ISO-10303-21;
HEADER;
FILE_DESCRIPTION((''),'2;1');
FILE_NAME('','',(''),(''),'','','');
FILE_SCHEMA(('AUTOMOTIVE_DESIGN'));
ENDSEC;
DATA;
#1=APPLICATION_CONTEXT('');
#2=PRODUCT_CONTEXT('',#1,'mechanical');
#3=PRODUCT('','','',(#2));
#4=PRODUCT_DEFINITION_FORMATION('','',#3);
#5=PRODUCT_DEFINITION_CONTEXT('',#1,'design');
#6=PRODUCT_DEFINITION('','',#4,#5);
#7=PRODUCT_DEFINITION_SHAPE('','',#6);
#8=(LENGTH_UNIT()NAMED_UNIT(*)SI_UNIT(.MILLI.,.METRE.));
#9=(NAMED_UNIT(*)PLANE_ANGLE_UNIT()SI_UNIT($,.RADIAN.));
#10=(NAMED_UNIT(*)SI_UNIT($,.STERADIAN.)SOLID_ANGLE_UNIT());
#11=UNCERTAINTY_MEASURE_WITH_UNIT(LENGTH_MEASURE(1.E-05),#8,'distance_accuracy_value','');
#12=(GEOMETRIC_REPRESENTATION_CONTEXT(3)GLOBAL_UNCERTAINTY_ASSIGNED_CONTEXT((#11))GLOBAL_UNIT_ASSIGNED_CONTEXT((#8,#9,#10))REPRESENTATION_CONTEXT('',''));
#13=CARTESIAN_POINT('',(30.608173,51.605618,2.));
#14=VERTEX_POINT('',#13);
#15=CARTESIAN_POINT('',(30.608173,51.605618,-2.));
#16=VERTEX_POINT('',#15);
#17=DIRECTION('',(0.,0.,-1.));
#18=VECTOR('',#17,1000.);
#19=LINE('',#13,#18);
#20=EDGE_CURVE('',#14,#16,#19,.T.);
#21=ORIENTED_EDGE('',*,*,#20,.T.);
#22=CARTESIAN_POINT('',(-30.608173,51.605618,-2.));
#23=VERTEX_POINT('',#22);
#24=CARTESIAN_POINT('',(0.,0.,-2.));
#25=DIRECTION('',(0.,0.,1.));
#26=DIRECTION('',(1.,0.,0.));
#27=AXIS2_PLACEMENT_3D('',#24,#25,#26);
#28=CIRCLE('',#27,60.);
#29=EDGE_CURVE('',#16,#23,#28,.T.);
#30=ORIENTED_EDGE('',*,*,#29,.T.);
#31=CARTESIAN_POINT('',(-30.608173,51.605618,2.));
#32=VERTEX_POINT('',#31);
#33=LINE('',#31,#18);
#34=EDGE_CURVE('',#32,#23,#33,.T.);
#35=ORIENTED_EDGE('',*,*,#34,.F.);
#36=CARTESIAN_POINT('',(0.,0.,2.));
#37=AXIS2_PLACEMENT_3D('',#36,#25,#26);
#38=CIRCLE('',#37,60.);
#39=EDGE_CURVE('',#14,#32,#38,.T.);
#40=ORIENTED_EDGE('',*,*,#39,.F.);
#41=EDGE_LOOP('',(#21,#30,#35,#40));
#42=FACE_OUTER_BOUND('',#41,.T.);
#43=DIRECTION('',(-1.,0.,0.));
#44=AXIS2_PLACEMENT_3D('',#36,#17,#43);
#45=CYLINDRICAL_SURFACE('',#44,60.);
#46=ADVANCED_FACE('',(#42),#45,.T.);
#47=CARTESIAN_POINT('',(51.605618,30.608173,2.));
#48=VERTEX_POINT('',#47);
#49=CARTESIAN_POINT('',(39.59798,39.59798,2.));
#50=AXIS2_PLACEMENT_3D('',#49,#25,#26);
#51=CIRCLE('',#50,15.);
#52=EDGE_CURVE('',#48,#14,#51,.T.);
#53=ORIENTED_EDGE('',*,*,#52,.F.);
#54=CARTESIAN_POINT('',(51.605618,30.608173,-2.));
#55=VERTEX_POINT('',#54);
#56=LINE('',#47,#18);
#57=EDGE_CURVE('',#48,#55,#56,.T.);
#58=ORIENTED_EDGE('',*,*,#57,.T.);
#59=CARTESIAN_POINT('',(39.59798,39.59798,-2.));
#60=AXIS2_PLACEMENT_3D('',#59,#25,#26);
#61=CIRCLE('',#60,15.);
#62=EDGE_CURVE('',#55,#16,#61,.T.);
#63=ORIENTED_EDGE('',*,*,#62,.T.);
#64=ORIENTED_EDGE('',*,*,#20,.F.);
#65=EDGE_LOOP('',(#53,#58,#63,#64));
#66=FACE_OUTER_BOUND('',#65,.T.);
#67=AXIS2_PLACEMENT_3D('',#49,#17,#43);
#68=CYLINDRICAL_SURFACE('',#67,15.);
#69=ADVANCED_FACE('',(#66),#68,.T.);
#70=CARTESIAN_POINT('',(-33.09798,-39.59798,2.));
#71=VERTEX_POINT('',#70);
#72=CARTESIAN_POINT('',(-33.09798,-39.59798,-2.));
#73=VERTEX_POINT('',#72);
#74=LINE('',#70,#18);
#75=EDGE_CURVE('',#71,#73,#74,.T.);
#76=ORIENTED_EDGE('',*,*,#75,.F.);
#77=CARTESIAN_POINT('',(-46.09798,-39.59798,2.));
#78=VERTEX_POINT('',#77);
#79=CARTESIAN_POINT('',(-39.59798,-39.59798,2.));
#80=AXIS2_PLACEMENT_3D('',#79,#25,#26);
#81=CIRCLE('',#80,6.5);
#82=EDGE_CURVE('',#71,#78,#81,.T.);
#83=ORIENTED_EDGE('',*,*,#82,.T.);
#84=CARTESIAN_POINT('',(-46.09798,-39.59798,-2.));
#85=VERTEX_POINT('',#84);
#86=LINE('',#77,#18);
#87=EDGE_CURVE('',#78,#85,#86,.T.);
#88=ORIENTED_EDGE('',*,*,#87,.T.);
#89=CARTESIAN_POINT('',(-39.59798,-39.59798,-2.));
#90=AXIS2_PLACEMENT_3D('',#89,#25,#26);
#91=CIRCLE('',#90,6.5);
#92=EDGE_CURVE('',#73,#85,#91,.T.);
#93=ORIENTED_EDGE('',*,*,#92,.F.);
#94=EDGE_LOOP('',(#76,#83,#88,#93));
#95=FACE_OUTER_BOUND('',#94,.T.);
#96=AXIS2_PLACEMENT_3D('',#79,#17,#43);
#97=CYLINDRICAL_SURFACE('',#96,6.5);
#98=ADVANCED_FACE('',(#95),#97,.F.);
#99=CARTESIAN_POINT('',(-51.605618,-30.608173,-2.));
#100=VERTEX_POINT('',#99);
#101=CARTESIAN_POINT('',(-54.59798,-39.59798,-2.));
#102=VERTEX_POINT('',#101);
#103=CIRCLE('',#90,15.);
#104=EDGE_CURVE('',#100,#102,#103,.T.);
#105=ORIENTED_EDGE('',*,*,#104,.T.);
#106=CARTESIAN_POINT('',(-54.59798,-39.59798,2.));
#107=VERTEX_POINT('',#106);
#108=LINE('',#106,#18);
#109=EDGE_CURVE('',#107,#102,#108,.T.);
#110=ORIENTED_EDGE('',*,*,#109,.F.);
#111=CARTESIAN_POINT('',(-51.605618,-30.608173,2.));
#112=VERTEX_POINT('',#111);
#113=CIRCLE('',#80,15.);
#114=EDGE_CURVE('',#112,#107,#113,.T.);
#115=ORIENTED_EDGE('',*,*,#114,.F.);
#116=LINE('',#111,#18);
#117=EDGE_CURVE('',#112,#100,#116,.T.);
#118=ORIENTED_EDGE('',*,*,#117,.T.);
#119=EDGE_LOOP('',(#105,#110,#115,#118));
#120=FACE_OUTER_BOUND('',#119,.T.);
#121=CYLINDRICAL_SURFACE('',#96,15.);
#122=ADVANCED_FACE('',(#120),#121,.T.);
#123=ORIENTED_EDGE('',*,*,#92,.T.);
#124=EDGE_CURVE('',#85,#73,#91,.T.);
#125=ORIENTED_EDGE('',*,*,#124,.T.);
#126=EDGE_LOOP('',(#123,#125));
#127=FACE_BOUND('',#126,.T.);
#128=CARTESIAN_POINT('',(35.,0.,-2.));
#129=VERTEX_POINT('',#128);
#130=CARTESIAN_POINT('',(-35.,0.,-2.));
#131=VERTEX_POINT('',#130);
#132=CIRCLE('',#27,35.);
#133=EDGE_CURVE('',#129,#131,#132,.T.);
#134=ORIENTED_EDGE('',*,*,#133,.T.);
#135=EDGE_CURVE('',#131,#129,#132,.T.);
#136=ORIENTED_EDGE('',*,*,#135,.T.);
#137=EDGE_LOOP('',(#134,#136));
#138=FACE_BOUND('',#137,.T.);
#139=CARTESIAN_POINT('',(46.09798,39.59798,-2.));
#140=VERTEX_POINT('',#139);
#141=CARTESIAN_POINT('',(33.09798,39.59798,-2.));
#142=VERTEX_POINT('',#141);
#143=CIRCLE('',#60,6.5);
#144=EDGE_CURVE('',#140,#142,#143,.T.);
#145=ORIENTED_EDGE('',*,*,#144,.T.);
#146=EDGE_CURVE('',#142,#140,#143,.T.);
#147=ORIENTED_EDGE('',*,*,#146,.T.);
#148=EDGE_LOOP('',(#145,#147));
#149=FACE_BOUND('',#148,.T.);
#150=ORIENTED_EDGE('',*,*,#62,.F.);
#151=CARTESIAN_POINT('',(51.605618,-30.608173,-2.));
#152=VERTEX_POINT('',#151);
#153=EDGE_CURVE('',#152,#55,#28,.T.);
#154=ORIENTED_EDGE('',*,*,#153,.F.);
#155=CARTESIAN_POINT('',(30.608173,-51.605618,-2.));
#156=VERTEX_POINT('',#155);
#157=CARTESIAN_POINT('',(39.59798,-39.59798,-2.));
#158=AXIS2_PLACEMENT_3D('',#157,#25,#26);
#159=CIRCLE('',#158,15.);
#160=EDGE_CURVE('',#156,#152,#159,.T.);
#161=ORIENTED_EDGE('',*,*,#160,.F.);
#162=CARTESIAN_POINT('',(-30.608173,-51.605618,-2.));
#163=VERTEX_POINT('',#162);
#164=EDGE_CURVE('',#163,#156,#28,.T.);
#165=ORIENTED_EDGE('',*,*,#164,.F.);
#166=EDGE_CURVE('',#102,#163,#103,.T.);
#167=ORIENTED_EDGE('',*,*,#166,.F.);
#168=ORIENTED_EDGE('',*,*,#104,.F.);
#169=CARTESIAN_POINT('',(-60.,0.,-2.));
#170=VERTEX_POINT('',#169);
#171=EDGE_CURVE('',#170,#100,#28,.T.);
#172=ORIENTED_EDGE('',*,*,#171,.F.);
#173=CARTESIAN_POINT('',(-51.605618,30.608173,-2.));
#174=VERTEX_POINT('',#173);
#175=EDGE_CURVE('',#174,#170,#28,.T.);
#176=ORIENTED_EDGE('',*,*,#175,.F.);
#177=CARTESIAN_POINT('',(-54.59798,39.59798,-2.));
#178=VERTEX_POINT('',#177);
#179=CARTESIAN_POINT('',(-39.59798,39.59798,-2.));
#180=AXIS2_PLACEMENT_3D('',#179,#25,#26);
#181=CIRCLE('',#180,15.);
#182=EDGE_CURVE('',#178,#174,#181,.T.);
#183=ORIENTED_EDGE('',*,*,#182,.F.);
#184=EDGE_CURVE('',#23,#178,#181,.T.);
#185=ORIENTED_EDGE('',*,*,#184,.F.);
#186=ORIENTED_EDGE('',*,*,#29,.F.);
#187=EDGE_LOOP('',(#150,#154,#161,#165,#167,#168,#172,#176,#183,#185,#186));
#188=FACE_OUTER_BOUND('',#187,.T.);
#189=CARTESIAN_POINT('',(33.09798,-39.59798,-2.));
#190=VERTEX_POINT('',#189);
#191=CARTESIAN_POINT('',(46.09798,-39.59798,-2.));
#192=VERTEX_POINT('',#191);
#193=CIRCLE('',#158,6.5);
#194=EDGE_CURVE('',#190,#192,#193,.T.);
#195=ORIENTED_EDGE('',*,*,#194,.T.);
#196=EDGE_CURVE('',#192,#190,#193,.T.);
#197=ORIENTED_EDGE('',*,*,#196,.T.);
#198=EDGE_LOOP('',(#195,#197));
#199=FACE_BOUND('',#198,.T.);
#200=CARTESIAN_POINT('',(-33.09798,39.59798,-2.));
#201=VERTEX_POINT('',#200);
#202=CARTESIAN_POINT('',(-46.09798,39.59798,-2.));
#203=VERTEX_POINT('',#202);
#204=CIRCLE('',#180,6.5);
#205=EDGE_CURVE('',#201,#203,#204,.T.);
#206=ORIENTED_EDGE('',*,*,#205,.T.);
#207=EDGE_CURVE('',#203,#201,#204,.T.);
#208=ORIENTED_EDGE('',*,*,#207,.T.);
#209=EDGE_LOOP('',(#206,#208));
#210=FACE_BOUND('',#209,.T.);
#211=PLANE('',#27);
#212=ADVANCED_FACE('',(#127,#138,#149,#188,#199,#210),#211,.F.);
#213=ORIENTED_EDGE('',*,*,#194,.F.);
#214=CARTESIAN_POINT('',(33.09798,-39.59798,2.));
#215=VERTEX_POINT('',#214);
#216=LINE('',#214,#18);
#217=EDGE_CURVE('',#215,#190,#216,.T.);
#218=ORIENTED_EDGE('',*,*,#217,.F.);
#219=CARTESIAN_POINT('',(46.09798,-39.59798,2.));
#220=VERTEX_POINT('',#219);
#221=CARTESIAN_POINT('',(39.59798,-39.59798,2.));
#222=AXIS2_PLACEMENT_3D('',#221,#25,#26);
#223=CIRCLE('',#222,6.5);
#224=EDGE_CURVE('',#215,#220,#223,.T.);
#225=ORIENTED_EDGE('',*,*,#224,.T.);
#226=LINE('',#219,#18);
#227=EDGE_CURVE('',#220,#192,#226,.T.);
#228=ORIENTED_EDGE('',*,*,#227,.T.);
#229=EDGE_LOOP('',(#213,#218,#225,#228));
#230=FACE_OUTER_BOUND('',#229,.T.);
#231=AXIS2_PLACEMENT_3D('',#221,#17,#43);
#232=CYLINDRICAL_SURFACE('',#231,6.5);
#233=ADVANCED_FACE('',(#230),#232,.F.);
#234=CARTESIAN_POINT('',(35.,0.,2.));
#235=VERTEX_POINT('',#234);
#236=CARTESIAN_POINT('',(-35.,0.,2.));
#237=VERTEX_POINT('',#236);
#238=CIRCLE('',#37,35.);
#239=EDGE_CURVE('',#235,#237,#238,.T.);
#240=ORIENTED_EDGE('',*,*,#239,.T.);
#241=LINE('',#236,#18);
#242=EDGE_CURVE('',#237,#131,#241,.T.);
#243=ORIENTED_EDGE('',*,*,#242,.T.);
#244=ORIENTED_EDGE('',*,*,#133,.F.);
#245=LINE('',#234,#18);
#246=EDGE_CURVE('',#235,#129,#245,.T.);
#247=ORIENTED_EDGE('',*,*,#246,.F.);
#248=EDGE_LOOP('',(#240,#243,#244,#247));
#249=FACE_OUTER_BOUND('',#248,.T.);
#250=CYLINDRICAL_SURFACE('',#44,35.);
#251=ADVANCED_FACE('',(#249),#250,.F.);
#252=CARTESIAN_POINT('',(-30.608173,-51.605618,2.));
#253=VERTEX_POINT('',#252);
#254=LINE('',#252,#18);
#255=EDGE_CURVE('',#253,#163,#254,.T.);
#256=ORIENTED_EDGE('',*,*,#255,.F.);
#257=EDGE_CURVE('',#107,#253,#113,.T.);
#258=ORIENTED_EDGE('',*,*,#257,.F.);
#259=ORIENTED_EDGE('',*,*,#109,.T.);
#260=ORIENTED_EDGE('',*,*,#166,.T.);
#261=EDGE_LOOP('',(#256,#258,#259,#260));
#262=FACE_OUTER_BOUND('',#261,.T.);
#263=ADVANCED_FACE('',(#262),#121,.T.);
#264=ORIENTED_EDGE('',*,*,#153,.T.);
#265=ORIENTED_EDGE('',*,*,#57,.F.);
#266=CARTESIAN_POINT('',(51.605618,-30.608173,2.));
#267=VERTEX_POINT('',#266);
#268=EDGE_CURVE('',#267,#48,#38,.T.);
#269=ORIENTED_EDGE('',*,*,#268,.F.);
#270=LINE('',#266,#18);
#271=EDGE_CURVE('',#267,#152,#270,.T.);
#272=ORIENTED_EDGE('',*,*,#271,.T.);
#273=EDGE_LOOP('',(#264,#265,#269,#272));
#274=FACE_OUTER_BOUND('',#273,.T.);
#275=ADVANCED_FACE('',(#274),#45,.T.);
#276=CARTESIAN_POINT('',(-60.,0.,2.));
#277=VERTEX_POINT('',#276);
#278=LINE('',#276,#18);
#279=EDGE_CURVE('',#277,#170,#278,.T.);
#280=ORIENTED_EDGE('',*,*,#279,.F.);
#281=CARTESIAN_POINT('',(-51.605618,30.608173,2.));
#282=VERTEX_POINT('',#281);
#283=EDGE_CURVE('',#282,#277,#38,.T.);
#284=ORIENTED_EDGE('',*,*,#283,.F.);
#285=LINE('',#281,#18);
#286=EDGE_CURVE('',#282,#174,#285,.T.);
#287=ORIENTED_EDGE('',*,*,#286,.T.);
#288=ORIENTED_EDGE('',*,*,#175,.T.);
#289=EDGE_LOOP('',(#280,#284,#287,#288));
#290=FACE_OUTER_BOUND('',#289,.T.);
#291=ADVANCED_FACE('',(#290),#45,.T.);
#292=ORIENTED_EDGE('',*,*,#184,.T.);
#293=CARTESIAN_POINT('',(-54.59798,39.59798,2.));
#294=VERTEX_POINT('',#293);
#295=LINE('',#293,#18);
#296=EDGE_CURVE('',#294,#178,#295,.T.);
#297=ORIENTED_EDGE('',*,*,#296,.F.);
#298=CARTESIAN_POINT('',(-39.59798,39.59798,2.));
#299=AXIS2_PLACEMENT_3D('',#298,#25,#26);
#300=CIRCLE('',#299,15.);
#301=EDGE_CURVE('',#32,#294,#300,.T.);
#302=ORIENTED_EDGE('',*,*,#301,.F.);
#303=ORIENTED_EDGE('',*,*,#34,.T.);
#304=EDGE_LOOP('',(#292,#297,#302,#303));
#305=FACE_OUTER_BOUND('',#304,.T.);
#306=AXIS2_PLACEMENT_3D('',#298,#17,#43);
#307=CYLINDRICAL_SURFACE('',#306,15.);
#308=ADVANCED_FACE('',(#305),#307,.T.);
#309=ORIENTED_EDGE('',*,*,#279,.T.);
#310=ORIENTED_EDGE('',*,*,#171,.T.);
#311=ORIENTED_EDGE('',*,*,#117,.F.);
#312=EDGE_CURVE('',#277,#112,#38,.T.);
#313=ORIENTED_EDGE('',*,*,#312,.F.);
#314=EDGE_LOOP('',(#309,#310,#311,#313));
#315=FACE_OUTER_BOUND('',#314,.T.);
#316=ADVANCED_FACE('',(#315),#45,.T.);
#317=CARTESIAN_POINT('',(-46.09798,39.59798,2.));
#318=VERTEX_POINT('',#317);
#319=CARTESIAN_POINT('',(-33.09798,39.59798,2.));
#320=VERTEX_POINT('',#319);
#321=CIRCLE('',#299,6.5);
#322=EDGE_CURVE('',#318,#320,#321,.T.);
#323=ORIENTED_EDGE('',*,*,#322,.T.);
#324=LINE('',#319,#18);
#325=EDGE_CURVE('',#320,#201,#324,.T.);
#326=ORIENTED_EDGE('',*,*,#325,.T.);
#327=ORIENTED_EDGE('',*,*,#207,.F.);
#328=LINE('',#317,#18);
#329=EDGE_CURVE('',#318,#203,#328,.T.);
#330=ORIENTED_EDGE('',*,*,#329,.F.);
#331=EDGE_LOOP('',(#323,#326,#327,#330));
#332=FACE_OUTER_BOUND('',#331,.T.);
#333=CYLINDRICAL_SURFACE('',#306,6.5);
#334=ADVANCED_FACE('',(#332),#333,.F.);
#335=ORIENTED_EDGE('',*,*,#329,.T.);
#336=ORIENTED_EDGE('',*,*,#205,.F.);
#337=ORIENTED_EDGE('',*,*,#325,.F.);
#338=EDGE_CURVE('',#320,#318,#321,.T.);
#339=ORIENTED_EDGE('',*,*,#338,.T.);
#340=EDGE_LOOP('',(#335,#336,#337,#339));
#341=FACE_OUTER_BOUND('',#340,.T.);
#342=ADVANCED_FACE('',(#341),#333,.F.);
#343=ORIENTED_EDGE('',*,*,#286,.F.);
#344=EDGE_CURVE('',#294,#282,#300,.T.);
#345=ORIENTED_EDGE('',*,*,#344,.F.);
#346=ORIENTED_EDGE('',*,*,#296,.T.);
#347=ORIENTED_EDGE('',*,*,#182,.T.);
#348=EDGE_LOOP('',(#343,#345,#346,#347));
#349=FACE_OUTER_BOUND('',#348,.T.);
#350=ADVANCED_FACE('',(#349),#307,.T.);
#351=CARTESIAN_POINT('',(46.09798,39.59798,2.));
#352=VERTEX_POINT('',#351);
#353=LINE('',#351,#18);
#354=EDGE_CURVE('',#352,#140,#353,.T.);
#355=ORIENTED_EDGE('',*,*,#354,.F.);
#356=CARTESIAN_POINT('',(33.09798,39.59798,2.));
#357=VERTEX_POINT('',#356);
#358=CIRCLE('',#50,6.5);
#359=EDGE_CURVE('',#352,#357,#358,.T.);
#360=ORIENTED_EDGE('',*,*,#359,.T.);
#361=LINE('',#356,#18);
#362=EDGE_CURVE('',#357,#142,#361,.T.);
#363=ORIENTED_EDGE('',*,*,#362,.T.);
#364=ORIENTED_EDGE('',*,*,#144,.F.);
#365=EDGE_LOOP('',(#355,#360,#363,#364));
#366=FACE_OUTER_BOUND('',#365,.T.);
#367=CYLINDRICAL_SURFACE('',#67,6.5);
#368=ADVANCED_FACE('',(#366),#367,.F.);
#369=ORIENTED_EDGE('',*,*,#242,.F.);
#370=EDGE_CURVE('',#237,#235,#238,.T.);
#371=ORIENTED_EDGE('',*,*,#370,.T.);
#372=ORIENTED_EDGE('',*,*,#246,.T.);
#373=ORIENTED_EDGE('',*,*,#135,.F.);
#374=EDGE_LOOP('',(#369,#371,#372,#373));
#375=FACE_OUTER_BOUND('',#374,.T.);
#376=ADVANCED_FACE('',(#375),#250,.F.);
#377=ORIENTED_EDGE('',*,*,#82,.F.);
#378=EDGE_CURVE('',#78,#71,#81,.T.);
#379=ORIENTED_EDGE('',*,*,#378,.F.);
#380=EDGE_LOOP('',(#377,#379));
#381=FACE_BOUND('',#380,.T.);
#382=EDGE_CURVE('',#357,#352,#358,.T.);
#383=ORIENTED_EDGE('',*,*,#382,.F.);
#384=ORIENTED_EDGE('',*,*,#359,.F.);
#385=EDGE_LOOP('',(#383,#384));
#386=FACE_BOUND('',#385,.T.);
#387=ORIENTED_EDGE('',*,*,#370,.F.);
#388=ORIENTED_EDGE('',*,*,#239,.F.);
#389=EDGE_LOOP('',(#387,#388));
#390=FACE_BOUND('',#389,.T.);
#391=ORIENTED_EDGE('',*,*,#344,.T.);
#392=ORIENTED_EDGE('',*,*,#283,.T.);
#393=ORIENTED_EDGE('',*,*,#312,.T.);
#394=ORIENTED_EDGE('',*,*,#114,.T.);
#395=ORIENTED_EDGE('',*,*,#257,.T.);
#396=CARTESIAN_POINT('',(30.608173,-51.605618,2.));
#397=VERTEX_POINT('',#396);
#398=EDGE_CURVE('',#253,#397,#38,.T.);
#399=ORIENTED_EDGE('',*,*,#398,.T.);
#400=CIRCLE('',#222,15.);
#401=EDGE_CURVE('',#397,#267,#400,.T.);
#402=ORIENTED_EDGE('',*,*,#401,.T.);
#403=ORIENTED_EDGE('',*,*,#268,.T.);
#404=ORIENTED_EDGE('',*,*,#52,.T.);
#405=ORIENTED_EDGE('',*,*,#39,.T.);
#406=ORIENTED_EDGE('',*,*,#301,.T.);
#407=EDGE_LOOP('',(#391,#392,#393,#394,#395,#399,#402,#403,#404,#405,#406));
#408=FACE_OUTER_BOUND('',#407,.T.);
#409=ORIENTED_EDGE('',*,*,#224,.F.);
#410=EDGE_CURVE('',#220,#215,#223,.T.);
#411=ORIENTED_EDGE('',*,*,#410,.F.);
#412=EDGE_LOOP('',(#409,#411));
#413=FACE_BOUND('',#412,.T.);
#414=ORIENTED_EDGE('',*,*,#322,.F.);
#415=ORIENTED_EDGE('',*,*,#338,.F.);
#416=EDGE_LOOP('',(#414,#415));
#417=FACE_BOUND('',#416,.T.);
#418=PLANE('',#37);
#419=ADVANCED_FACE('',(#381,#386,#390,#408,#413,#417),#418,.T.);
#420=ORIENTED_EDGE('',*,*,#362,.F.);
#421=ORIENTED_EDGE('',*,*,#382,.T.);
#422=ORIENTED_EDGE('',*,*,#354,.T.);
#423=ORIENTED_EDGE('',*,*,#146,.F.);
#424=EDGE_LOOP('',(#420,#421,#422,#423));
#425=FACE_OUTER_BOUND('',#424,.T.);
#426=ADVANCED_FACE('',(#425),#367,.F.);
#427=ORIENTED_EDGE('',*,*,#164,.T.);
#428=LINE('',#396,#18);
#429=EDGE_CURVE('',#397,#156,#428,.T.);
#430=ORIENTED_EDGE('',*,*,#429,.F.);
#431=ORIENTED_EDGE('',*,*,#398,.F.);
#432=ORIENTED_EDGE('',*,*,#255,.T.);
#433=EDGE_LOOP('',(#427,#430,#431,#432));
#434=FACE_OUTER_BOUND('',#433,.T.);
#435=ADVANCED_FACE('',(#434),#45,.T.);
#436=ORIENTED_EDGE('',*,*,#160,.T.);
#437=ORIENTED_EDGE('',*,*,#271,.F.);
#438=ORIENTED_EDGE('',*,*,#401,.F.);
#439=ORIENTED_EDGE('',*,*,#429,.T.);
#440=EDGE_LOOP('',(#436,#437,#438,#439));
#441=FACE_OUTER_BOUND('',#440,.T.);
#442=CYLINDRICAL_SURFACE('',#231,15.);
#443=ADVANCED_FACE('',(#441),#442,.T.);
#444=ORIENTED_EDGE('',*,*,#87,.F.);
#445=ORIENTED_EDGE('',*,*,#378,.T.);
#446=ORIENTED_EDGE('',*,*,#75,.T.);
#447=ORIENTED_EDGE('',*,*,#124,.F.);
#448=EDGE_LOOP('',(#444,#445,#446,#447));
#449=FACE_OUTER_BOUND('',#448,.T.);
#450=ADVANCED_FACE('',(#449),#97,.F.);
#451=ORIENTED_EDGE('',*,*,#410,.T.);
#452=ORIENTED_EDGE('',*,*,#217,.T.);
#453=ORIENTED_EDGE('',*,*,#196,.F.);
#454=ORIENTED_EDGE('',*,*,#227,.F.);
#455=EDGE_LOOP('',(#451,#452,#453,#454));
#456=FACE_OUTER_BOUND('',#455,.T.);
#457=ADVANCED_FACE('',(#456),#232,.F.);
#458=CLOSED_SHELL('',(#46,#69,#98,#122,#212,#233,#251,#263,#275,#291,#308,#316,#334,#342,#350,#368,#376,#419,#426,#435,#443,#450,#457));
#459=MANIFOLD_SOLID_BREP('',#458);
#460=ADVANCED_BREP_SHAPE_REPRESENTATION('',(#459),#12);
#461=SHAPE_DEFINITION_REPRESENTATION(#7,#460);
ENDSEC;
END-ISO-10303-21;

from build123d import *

# Parameters (mm, degrees)
SKETCH1_R           = 35
SKETCH1_R_2         = 6.5
BOSS_EXTRUDE1_DEPTH = 2


with BuildPart() as part:
    # Sketch1 → Boss-Extrude1 (new, symmetric)
    with BuildSketch(Plane.XY):
        with BuildLine():
            ThreePointArc((30.608172596, 51.605617624), (0, 60), (-30.608172596, 51.605617624))
            ThreePointArc((-30.608172596, 51.605617624), (-50.204581464, 50.204581464), (-51.605617624, 30.608172596))
            ThreePointArc((-51.605617624, 30.608172596), (-60, 0), (-51.605617624, -30.608172596))
            ThreePointArc((-51.605617624, -30.608172596), (-50.204581464, -50.204581464), (-30.608172596, -51.605617624))
            ThreePointArc((-30.608172596, -51.605617624), (0, -60), (30.608172596, -51.605617624))
            ThreePointArc((30.608172596, -51.605617624), (50.204581464, -50.204581464), (51.605617624, -30.608172596))
            ThreePointArc((51.605617624, -30.608172596), (60, 0), (51.605617624, 30.608172596))
            ThreePointArc((51.605617624, 30.608172596), (50.204581464, 50.204581464), (30.608172596, 51.605617624))
        make_face()
        Circle(SKETCH1_R, mode=Mode.SUBTRACT)
        with Locations((39.597979746, 39.597979746)):
            Circle(SKETCH1_R_2, mode=Mode.SUBTRACT)
        with Locations((39.597979746, -39.597979746)):
            Circle(SKETCH1_R_2, mode=Mode.SUBTRACT)
        with Locations((-39.597979746, -39.597979746)):
            Circle(SKETCH1_R_2, mode=Mode.SUBTRACT)
        with Locations((-39.597979746, 39.597979746)):
            Circle(SKETCH1_R_2, mode=Mode.SUBTRACT)
    extrude(amount=BOSS_EXTRUDE1_DEPTH, both=True)


solid = part.part
